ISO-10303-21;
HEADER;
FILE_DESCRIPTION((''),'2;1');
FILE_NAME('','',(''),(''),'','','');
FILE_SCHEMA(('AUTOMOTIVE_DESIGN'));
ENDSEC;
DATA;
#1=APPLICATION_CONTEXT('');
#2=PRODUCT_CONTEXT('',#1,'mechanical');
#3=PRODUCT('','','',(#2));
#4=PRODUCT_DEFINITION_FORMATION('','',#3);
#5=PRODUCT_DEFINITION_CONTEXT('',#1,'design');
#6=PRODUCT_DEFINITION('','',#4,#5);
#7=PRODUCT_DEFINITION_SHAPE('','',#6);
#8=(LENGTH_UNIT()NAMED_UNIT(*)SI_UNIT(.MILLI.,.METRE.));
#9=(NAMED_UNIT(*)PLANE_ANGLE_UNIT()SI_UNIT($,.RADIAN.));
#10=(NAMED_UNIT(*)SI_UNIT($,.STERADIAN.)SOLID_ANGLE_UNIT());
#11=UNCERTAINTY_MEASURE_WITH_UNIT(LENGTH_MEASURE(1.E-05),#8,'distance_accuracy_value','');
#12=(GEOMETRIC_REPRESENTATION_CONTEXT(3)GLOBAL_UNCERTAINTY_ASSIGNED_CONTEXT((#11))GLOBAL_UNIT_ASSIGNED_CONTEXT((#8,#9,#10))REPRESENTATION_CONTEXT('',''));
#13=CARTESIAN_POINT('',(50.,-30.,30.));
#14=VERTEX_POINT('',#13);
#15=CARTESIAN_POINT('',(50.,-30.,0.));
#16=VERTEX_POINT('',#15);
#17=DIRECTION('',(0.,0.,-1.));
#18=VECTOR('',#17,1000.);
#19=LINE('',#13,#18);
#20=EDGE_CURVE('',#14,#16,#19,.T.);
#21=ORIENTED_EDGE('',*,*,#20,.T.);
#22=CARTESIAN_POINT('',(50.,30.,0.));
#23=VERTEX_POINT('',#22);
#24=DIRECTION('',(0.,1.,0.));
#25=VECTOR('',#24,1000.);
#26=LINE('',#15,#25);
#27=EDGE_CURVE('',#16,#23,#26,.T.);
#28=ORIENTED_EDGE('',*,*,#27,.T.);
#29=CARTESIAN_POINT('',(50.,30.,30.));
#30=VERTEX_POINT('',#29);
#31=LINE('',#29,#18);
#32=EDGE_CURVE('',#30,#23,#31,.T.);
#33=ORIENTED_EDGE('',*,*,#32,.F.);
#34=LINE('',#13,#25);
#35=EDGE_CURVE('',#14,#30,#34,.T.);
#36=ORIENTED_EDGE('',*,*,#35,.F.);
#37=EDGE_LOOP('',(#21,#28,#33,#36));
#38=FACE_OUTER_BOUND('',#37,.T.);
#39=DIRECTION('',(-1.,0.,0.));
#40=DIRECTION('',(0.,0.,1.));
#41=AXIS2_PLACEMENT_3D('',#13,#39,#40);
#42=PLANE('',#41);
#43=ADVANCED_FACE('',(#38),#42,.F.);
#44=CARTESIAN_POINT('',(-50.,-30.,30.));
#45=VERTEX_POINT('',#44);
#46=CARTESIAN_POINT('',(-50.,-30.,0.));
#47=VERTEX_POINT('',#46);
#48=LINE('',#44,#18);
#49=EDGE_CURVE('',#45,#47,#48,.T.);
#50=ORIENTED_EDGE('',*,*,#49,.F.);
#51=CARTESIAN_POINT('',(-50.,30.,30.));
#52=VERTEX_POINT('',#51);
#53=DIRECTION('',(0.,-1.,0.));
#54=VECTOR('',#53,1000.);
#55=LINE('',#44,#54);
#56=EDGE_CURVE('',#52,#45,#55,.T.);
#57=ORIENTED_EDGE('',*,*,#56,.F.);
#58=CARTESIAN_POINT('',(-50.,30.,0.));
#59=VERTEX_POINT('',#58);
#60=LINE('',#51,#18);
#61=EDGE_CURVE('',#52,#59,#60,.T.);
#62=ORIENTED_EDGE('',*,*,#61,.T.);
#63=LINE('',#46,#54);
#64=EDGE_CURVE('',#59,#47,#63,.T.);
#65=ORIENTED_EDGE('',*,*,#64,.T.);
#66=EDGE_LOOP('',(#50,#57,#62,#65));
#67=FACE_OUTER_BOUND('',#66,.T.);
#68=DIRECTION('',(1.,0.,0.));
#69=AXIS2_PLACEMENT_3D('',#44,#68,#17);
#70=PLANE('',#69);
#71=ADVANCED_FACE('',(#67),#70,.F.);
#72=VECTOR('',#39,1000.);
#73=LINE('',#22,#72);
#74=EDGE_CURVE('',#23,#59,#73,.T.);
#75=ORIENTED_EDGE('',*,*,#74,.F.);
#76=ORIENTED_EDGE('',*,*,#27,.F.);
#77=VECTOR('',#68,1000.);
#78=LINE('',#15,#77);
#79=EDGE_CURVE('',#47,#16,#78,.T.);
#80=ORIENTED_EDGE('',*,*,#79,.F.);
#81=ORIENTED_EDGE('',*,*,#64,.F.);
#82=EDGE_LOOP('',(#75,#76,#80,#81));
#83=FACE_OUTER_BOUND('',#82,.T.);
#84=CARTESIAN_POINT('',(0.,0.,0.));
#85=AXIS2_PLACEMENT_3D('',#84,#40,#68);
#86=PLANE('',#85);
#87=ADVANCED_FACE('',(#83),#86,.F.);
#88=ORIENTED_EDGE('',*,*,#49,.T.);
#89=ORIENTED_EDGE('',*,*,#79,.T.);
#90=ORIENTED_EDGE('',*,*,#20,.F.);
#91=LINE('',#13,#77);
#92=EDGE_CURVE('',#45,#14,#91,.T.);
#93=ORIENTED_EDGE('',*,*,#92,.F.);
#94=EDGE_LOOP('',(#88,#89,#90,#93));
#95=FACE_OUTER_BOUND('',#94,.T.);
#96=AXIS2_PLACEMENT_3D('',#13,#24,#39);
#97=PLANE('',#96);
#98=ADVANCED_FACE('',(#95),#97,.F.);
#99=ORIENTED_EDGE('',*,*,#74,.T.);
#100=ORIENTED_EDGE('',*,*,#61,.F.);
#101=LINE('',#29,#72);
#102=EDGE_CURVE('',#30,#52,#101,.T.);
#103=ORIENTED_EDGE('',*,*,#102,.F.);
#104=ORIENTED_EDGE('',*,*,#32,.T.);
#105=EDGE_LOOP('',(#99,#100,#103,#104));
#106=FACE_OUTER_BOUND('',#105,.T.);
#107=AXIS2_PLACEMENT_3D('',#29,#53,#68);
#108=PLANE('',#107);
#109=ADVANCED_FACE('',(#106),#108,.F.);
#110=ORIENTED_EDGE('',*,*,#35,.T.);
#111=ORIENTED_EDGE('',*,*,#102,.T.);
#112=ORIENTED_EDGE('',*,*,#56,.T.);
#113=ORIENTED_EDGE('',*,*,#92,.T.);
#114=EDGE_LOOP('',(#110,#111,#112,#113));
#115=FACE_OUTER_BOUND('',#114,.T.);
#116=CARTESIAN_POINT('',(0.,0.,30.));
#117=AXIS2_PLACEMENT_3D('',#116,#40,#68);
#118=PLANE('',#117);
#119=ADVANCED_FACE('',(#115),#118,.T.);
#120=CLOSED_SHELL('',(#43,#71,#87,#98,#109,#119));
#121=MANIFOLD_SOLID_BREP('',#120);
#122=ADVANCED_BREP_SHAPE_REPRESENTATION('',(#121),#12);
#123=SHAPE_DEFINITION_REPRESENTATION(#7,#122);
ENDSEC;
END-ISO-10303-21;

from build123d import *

# Parameters (mm, degrees)
SKETCH1_W           = 100
SKETCH1_H           = 60
BOSS_EXTRUDE1_DEPTH = 30


with BuildPart() as part:
    # Sketch1 → Boss-Extrude1 (new body)
    with BuildSketch(Plane.XY):
        Rectangle(SKETCH1_W, SKETCH1_H)
    extrude(amount=BOSS_EXTRUDE1_DEPTH)


solid = part.part
